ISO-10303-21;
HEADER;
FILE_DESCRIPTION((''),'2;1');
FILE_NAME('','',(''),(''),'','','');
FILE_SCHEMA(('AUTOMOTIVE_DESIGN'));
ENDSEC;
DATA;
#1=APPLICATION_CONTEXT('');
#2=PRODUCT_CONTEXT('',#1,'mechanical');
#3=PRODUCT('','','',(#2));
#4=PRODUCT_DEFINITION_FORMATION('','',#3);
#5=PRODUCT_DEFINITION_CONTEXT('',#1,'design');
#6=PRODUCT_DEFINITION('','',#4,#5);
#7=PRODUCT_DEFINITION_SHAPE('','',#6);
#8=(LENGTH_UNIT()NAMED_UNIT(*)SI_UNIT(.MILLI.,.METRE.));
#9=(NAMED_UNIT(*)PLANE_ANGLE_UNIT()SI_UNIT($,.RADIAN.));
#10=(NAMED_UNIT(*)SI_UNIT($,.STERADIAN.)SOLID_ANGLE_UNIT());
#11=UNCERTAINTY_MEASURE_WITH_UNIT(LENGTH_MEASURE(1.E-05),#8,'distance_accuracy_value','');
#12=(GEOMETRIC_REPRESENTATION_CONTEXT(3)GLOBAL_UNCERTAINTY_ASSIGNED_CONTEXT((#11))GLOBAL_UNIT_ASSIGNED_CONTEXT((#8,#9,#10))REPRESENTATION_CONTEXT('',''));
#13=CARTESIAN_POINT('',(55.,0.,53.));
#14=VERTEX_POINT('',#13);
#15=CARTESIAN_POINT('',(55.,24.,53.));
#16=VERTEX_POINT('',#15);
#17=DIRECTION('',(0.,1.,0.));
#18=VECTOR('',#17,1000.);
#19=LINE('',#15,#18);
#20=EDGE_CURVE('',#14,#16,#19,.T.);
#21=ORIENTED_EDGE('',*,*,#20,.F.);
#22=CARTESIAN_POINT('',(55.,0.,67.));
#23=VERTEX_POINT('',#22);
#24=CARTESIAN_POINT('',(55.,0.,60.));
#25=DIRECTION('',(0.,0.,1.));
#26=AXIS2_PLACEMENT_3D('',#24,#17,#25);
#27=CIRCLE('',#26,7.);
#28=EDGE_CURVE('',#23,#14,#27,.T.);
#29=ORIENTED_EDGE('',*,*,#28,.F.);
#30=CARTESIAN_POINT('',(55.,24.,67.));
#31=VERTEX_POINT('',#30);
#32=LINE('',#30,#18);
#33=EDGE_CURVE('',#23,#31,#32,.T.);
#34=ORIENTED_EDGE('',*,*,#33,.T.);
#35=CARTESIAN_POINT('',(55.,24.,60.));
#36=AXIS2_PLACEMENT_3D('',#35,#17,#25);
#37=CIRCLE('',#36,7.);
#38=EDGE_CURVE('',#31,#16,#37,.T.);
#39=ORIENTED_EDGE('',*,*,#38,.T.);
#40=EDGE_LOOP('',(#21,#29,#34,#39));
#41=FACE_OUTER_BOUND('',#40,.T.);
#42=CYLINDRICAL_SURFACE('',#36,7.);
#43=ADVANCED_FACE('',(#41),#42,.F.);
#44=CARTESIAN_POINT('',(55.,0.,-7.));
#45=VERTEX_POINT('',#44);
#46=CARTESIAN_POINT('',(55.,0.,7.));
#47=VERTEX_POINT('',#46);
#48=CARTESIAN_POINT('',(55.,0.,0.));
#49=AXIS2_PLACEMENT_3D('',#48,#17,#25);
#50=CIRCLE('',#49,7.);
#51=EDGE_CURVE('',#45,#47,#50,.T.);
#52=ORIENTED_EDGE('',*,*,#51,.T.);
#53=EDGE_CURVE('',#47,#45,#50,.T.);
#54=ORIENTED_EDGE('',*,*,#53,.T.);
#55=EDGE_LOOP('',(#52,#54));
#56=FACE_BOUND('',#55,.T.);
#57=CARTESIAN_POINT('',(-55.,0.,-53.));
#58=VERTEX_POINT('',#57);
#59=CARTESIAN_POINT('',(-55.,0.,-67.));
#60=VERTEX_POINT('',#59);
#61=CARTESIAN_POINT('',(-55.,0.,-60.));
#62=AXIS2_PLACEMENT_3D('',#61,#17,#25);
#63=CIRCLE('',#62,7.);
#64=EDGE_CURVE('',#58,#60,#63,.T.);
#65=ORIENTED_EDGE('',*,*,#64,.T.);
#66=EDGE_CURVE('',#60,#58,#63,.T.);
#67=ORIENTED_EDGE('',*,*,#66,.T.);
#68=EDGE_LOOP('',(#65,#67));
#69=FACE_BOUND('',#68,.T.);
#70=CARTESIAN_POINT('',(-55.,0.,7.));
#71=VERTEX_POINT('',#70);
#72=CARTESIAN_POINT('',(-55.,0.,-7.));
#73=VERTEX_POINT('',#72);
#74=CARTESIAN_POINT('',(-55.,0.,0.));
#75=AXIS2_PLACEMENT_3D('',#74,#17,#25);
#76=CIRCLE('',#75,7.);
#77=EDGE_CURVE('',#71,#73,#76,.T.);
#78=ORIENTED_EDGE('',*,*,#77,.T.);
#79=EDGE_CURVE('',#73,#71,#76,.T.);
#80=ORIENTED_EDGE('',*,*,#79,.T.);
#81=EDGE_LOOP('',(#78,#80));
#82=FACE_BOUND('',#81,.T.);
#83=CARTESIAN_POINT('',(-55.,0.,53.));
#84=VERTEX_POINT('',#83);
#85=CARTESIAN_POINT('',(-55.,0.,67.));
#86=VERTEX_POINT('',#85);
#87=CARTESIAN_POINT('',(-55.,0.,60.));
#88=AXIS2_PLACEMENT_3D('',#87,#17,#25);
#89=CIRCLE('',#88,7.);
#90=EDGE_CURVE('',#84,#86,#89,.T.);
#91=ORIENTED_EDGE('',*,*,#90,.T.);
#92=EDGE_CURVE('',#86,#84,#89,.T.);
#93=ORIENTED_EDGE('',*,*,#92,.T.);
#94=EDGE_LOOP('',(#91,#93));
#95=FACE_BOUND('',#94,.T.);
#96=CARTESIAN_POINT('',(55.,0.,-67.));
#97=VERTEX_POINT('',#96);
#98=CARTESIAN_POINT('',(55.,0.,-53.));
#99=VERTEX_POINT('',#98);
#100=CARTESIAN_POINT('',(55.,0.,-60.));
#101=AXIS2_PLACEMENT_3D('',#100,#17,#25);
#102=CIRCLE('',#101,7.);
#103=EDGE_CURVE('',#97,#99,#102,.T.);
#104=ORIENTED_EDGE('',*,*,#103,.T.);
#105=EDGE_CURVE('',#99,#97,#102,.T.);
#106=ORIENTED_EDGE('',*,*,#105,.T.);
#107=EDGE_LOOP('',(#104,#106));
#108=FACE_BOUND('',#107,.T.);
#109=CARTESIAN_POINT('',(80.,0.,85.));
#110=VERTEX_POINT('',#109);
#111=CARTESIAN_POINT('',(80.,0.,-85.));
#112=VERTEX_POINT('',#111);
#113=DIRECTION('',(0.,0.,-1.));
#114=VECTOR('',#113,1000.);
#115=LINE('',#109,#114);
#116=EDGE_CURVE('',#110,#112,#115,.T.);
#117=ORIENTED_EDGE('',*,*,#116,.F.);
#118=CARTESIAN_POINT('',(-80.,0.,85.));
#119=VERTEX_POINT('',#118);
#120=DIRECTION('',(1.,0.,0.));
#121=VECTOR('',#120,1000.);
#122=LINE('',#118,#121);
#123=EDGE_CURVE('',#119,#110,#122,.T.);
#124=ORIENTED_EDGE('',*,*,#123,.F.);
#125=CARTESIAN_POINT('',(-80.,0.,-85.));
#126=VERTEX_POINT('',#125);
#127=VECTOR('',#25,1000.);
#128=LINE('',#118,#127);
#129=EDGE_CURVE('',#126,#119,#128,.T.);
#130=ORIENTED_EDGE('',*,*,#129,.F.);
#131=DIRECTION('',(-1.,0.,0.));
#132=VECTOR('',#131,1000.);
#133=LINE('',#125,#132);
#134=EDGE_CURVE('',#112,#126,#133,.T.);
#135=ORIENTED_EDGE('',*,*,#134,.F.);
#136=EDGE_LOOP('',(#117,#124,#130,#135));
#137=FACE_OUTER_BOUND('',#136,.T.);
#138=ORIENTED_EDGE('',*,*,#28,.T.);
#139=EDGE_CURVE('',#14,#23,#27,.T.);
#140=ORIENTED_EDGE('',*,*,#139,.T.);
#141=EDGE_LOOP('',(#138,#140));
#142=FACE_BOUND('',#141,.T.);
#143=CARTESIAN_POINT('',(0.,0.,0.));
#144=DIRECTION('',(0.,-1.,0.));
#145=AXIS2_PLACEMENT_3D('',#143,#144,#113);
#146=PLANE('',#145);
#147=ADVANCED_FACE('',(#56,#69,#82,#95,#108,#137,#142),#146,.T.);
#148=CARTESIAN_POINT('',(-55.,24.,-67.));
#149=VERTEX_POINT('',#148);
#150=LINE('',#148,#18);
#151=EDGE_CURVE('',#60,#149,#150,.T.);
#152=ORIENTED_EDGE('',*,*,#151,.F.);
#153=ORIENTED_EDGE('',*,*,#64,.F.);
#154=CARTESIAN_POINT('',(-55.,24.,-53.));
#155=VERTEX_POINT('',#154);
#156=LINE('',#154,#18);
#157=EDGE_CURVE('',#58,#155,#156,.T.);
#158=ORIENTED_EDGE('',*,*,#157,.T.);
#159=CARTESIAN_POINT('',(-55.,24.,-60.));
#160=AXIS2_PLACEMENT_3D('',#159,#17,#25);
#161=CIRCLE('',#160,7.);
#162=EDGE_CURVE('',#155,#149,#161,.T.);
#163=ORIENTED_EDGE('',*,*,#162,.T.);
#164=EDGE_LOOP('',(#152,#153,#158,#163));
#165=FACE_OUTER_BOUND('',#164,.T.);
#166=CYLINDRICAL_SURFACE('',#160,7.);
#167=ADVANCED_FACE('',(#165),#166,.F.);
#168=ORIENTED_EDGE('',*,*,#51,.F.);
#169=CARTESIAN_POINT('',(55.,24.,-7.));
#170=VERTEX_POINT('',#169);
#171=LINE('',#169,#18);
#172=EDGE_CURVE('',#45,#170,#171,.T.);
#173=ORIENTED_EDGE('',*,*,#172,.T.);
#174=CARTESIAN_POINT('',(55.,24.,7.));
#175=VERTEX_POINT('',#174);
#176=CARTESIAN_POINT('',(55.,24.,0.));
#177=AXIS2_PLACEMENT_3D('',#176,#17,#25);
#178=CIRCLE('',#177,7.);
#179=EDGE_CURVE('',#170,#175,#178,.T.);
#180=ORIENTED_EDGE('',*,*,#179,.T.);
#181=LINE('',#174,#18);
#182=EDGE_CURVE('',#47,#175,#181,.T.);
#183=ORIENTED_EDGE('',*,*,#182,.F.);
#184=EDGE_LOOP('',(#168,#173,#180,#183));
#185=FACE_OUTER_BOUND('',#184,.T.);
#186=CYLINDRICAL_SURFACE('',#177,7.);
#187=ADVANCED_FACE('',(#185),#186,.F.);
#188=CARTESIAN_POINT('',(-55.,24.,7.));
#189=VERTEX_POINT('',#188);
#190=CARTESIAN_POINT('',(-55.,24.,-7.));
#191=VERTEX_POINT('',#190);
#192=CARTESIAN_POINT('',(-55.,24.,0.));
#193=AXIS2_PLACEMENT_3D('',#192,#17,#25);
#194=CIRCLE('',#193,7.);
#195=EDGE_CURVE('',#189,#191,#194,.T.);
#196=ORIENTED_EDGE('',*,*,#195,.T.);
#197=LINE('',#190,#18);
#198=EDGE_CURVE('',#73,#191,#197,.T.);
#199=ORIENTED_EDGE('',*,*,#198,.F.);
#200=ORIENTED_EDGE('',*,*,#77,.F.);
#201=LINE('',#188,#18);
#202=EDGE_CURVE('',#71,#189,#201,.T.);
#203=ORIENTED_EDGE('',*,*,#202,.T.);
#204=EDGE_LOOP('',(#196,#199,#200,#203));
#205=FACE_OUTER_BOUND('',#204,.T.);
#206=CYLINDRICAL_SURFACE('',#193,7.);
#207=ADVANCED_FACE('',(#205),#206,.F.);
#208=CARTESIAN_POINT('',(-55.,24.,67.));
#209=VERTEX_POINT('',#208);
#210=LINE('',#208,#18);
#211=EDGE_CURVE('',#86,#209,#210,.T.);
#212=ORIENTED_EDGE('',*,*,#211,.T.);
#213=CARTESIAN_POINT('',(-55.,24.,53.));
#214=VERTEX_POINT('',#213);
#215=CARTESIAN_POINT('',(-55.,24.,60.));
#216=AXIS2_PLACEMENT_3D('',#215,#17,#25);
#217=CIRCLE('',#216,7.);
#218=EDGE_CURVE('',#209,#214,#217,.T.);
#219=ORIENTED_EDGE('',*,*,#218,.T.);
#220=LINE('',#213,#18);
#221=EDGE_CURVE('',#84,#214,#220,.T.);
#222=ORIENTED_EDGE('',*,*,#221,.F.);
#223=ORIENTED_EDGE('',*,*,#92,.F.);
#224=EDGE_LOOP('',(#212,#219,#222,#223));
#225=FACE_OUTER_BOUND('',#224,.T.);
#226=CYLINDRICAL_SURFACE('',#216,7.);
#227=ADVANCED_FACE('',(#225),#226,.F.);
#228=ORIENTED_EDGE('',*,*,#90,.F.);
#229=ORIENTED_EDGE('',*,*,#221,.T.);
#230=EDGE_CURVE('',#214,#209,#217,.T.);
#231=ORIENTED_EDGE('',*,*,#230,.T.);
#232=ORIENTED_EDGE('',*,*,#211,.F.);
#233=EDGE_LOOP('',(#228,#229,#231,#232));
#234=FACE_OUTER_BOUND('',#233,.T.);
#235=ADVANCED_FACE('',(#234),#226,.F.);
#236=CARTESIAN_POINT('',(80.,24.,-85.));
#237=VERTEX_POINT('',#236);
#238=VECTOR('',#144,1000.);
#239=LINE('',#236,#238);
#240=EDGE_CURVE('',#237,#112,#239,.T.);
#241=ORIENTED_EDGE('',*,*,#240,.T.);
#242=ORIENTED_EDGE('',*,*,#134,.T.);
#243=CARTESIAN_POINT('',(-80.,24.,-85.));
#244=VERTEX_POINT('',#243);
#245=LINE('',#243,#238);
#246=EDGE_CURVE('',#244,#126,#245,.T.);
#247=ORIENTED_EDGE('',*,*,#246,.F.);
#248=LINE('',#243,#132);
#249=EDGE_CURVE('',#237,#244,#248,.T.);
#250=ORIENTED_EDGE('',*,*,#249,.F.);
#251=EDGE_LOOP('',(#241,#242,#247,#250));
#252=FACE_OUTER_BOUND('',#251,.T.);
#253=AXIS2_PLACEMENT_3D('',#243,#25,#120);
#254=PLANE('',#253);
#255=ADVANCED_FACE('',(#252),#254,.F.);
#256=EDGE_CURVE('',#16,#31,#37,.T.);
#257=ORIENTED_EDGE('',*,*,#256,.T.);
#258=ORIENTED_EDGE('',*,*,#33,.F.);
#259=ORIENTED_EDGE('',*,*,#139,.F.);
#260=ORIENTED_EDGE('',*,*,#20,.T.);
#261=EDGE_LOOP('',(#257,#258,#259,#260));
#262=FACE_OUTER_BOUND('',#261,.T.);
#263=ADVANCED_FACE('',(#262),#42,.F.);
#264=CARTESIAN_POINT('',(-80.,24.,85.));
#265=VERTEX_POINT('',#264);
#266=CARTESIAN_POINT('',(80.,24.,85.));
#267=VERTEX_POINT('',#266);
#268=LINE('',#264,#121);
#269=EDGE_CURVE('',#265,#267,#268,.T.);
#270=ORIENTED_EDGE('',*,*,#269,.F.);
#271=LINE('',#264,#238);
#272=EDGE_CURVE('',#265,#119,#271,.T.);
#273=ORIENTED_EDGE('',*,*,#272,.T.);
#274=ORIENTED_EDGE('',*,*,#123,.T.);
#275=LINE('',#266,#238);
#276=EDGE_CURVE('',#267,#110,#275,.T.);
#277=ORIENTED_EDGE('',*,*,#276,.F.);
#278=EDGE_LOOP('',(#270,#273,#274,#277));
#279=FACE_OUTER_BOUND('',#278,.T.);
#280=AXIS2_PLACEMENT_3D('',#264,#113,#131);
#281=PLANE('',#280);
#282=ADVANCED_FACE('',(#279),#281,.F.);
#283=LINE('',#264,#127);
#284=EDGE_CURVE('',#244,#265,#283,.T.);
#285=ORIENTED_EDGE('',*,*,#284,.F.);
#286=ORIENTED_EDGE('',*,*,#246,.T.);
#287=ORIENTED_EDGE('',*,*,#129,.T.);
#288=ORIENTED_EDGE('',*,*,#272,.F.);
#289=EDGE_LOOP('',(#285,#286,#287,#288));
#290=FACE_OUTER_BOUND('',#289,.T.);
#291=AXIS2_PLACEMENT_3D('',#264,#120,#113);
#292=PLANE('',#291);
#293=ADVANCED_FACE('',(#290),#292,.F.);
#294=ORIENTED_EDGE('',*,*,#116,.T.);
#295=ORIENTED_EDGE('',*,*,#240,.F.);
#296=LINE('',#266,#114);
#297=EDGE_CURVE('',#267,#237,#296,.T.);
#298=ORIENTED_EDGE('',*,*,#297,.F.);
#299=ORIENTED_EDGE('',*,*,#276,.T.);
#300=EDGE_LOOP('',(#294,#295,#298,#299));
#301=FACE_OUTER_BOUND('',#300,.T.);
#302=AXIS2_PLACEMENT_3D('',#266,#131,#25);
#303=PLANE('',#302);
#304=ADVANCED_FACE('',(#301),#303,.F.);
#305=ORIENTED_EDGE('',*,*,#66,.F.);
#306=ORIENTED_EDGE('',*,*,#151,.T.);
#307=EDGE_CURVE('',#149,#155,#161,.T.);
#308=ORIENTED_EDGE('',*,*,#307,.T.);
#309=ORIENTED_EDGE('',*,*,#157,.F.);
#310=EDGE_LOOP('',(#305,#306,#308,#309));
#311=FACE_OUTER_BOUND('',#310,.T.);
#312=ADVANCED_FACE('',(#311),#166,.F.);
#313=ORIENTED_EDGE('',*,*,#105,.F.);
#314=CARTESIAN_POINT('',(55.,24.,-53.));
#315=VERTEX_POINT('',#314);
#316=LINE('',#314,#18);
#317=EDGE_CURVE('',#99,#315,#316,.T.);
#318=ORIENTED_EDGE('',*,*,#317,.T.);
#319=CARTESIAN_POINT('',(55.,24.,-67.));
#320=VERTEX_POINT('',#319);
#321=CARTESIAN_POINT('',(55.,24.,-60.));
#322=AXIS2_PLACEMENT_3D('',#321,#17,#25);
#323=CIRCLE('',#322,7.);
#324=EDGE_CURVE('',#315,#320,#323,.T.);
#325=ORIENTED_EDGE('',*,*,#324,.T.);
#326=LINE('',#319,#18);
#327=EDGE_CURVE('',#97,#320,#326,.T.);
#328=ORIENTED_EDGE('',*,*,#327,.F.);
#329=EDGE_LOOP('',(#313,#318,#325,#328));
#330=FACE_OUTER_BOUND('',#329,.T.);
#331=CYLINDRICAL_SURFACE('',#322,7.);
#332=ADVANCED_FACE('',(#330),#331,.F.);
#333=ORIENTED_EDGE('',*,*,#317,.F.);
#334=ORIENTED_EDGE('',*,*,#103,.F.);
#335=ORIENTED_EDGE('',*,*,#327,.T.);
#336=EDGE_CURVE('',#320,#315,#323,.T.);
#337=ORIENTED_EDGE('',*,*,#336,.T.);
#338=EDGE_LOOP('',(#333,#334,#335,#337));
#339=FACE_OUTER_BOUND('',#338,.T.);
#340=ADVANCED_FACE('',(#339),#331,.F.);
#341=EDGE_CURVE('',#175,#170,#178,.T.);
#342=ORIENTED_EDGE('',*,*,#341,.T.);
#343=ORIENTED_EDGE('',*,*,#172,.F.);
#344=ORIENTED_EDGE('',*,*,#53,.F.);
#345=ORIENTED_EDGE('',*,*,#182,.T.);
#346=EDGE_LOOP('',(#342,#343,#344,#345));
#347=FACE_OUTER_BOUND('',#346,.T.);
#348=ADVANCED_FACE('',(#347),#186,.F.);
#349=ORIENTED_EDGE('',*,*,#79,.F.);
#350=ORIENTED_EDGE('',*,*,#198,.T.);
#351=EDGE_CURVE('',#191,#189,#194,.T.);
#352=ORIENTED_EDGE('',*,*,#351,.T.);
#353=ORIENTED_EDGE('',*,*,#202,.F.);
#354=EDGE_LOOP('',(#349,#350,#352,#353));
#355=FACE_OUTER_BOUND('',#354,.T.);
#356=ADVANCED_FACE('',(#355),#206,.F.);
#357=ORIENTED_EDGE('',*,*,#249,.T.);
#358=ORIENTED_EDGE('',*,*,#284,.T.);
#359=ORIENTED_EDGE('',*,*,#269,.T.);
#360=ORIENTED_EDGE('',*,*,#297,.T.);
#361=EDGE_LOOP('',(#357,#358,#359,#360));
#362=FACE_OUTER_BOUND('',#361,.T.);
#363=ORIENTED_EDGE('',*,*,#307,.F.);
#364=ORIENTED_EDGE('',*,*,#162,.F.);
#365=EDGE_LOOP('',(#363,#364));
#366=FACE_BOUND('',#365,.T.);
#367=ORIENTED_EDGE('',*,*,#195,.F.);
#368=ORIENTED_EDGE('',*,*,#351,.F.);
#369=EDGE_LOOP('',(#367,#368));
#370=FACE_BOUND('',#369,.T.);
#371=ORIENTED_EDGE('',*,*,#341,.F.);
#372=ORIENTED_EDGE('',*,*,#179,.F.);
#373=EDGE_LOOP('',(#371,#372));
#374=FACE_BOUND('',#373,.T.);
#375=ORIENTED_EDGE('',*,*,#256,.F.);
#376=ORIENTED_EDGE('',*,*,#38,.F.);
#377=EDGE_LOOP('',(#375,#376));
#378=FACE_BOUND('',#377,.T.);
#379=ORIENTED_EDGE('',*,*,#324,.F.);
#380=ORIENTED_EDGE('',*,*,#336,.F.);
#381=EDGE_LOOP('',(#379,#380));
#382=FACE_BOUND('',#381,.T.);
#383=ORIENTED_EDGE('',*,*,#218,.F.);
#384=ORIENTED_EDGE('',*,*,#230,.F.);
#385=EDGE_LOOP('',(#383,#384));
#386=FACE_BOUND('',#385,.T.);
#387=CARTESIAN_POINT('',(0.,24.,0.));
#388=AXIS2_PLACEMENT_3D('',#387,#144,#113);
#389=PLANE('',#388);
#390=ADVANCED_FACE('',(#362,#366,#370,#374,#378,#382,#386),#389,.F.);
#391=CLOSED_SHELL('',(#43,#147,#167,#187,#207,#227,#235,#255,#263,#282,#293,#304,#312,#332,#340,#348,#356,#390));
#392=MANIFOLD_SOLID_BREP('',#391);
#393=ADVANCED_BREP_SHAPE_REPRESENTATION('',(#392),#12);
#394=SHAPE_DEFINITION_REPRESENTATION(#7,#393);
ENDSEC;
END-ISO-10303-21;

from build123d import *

# Parameters (mm, degrees)
SKETCH_1_W          = 160
SKETCH_1_H          = 170
EXTRUDE_1_DEPTH     = 24
HOLE_WIZARD_M16_1_D = 14


with BuildPart() as part:
    # 草图1 → 凸台-拉伸1 (new body)
    with BuildSketch(Plane(origin=(0, 0, 0), x_dir=(1, 0, 0), z_dir=(0, 1, 0))):
        Rectangle(SKETCH_1_W, SKETCH_1_H)
    extrude(amount=EXTRUDE_1_DEPTH)

    # M16 螺纹孔1 (through all)
    with Locations(Plane(origin=(0, 24, 0), x_dir=(1, 0, 0), z_dir=(0, 1, 0))):
        with Locations((-55, -60), (-55, 60), (55, 60), (55, -60), (55, 0), (-55, 0)):
            Hole(HOLE_WIZARD_M16_1_D / 2)


solid = part.part
